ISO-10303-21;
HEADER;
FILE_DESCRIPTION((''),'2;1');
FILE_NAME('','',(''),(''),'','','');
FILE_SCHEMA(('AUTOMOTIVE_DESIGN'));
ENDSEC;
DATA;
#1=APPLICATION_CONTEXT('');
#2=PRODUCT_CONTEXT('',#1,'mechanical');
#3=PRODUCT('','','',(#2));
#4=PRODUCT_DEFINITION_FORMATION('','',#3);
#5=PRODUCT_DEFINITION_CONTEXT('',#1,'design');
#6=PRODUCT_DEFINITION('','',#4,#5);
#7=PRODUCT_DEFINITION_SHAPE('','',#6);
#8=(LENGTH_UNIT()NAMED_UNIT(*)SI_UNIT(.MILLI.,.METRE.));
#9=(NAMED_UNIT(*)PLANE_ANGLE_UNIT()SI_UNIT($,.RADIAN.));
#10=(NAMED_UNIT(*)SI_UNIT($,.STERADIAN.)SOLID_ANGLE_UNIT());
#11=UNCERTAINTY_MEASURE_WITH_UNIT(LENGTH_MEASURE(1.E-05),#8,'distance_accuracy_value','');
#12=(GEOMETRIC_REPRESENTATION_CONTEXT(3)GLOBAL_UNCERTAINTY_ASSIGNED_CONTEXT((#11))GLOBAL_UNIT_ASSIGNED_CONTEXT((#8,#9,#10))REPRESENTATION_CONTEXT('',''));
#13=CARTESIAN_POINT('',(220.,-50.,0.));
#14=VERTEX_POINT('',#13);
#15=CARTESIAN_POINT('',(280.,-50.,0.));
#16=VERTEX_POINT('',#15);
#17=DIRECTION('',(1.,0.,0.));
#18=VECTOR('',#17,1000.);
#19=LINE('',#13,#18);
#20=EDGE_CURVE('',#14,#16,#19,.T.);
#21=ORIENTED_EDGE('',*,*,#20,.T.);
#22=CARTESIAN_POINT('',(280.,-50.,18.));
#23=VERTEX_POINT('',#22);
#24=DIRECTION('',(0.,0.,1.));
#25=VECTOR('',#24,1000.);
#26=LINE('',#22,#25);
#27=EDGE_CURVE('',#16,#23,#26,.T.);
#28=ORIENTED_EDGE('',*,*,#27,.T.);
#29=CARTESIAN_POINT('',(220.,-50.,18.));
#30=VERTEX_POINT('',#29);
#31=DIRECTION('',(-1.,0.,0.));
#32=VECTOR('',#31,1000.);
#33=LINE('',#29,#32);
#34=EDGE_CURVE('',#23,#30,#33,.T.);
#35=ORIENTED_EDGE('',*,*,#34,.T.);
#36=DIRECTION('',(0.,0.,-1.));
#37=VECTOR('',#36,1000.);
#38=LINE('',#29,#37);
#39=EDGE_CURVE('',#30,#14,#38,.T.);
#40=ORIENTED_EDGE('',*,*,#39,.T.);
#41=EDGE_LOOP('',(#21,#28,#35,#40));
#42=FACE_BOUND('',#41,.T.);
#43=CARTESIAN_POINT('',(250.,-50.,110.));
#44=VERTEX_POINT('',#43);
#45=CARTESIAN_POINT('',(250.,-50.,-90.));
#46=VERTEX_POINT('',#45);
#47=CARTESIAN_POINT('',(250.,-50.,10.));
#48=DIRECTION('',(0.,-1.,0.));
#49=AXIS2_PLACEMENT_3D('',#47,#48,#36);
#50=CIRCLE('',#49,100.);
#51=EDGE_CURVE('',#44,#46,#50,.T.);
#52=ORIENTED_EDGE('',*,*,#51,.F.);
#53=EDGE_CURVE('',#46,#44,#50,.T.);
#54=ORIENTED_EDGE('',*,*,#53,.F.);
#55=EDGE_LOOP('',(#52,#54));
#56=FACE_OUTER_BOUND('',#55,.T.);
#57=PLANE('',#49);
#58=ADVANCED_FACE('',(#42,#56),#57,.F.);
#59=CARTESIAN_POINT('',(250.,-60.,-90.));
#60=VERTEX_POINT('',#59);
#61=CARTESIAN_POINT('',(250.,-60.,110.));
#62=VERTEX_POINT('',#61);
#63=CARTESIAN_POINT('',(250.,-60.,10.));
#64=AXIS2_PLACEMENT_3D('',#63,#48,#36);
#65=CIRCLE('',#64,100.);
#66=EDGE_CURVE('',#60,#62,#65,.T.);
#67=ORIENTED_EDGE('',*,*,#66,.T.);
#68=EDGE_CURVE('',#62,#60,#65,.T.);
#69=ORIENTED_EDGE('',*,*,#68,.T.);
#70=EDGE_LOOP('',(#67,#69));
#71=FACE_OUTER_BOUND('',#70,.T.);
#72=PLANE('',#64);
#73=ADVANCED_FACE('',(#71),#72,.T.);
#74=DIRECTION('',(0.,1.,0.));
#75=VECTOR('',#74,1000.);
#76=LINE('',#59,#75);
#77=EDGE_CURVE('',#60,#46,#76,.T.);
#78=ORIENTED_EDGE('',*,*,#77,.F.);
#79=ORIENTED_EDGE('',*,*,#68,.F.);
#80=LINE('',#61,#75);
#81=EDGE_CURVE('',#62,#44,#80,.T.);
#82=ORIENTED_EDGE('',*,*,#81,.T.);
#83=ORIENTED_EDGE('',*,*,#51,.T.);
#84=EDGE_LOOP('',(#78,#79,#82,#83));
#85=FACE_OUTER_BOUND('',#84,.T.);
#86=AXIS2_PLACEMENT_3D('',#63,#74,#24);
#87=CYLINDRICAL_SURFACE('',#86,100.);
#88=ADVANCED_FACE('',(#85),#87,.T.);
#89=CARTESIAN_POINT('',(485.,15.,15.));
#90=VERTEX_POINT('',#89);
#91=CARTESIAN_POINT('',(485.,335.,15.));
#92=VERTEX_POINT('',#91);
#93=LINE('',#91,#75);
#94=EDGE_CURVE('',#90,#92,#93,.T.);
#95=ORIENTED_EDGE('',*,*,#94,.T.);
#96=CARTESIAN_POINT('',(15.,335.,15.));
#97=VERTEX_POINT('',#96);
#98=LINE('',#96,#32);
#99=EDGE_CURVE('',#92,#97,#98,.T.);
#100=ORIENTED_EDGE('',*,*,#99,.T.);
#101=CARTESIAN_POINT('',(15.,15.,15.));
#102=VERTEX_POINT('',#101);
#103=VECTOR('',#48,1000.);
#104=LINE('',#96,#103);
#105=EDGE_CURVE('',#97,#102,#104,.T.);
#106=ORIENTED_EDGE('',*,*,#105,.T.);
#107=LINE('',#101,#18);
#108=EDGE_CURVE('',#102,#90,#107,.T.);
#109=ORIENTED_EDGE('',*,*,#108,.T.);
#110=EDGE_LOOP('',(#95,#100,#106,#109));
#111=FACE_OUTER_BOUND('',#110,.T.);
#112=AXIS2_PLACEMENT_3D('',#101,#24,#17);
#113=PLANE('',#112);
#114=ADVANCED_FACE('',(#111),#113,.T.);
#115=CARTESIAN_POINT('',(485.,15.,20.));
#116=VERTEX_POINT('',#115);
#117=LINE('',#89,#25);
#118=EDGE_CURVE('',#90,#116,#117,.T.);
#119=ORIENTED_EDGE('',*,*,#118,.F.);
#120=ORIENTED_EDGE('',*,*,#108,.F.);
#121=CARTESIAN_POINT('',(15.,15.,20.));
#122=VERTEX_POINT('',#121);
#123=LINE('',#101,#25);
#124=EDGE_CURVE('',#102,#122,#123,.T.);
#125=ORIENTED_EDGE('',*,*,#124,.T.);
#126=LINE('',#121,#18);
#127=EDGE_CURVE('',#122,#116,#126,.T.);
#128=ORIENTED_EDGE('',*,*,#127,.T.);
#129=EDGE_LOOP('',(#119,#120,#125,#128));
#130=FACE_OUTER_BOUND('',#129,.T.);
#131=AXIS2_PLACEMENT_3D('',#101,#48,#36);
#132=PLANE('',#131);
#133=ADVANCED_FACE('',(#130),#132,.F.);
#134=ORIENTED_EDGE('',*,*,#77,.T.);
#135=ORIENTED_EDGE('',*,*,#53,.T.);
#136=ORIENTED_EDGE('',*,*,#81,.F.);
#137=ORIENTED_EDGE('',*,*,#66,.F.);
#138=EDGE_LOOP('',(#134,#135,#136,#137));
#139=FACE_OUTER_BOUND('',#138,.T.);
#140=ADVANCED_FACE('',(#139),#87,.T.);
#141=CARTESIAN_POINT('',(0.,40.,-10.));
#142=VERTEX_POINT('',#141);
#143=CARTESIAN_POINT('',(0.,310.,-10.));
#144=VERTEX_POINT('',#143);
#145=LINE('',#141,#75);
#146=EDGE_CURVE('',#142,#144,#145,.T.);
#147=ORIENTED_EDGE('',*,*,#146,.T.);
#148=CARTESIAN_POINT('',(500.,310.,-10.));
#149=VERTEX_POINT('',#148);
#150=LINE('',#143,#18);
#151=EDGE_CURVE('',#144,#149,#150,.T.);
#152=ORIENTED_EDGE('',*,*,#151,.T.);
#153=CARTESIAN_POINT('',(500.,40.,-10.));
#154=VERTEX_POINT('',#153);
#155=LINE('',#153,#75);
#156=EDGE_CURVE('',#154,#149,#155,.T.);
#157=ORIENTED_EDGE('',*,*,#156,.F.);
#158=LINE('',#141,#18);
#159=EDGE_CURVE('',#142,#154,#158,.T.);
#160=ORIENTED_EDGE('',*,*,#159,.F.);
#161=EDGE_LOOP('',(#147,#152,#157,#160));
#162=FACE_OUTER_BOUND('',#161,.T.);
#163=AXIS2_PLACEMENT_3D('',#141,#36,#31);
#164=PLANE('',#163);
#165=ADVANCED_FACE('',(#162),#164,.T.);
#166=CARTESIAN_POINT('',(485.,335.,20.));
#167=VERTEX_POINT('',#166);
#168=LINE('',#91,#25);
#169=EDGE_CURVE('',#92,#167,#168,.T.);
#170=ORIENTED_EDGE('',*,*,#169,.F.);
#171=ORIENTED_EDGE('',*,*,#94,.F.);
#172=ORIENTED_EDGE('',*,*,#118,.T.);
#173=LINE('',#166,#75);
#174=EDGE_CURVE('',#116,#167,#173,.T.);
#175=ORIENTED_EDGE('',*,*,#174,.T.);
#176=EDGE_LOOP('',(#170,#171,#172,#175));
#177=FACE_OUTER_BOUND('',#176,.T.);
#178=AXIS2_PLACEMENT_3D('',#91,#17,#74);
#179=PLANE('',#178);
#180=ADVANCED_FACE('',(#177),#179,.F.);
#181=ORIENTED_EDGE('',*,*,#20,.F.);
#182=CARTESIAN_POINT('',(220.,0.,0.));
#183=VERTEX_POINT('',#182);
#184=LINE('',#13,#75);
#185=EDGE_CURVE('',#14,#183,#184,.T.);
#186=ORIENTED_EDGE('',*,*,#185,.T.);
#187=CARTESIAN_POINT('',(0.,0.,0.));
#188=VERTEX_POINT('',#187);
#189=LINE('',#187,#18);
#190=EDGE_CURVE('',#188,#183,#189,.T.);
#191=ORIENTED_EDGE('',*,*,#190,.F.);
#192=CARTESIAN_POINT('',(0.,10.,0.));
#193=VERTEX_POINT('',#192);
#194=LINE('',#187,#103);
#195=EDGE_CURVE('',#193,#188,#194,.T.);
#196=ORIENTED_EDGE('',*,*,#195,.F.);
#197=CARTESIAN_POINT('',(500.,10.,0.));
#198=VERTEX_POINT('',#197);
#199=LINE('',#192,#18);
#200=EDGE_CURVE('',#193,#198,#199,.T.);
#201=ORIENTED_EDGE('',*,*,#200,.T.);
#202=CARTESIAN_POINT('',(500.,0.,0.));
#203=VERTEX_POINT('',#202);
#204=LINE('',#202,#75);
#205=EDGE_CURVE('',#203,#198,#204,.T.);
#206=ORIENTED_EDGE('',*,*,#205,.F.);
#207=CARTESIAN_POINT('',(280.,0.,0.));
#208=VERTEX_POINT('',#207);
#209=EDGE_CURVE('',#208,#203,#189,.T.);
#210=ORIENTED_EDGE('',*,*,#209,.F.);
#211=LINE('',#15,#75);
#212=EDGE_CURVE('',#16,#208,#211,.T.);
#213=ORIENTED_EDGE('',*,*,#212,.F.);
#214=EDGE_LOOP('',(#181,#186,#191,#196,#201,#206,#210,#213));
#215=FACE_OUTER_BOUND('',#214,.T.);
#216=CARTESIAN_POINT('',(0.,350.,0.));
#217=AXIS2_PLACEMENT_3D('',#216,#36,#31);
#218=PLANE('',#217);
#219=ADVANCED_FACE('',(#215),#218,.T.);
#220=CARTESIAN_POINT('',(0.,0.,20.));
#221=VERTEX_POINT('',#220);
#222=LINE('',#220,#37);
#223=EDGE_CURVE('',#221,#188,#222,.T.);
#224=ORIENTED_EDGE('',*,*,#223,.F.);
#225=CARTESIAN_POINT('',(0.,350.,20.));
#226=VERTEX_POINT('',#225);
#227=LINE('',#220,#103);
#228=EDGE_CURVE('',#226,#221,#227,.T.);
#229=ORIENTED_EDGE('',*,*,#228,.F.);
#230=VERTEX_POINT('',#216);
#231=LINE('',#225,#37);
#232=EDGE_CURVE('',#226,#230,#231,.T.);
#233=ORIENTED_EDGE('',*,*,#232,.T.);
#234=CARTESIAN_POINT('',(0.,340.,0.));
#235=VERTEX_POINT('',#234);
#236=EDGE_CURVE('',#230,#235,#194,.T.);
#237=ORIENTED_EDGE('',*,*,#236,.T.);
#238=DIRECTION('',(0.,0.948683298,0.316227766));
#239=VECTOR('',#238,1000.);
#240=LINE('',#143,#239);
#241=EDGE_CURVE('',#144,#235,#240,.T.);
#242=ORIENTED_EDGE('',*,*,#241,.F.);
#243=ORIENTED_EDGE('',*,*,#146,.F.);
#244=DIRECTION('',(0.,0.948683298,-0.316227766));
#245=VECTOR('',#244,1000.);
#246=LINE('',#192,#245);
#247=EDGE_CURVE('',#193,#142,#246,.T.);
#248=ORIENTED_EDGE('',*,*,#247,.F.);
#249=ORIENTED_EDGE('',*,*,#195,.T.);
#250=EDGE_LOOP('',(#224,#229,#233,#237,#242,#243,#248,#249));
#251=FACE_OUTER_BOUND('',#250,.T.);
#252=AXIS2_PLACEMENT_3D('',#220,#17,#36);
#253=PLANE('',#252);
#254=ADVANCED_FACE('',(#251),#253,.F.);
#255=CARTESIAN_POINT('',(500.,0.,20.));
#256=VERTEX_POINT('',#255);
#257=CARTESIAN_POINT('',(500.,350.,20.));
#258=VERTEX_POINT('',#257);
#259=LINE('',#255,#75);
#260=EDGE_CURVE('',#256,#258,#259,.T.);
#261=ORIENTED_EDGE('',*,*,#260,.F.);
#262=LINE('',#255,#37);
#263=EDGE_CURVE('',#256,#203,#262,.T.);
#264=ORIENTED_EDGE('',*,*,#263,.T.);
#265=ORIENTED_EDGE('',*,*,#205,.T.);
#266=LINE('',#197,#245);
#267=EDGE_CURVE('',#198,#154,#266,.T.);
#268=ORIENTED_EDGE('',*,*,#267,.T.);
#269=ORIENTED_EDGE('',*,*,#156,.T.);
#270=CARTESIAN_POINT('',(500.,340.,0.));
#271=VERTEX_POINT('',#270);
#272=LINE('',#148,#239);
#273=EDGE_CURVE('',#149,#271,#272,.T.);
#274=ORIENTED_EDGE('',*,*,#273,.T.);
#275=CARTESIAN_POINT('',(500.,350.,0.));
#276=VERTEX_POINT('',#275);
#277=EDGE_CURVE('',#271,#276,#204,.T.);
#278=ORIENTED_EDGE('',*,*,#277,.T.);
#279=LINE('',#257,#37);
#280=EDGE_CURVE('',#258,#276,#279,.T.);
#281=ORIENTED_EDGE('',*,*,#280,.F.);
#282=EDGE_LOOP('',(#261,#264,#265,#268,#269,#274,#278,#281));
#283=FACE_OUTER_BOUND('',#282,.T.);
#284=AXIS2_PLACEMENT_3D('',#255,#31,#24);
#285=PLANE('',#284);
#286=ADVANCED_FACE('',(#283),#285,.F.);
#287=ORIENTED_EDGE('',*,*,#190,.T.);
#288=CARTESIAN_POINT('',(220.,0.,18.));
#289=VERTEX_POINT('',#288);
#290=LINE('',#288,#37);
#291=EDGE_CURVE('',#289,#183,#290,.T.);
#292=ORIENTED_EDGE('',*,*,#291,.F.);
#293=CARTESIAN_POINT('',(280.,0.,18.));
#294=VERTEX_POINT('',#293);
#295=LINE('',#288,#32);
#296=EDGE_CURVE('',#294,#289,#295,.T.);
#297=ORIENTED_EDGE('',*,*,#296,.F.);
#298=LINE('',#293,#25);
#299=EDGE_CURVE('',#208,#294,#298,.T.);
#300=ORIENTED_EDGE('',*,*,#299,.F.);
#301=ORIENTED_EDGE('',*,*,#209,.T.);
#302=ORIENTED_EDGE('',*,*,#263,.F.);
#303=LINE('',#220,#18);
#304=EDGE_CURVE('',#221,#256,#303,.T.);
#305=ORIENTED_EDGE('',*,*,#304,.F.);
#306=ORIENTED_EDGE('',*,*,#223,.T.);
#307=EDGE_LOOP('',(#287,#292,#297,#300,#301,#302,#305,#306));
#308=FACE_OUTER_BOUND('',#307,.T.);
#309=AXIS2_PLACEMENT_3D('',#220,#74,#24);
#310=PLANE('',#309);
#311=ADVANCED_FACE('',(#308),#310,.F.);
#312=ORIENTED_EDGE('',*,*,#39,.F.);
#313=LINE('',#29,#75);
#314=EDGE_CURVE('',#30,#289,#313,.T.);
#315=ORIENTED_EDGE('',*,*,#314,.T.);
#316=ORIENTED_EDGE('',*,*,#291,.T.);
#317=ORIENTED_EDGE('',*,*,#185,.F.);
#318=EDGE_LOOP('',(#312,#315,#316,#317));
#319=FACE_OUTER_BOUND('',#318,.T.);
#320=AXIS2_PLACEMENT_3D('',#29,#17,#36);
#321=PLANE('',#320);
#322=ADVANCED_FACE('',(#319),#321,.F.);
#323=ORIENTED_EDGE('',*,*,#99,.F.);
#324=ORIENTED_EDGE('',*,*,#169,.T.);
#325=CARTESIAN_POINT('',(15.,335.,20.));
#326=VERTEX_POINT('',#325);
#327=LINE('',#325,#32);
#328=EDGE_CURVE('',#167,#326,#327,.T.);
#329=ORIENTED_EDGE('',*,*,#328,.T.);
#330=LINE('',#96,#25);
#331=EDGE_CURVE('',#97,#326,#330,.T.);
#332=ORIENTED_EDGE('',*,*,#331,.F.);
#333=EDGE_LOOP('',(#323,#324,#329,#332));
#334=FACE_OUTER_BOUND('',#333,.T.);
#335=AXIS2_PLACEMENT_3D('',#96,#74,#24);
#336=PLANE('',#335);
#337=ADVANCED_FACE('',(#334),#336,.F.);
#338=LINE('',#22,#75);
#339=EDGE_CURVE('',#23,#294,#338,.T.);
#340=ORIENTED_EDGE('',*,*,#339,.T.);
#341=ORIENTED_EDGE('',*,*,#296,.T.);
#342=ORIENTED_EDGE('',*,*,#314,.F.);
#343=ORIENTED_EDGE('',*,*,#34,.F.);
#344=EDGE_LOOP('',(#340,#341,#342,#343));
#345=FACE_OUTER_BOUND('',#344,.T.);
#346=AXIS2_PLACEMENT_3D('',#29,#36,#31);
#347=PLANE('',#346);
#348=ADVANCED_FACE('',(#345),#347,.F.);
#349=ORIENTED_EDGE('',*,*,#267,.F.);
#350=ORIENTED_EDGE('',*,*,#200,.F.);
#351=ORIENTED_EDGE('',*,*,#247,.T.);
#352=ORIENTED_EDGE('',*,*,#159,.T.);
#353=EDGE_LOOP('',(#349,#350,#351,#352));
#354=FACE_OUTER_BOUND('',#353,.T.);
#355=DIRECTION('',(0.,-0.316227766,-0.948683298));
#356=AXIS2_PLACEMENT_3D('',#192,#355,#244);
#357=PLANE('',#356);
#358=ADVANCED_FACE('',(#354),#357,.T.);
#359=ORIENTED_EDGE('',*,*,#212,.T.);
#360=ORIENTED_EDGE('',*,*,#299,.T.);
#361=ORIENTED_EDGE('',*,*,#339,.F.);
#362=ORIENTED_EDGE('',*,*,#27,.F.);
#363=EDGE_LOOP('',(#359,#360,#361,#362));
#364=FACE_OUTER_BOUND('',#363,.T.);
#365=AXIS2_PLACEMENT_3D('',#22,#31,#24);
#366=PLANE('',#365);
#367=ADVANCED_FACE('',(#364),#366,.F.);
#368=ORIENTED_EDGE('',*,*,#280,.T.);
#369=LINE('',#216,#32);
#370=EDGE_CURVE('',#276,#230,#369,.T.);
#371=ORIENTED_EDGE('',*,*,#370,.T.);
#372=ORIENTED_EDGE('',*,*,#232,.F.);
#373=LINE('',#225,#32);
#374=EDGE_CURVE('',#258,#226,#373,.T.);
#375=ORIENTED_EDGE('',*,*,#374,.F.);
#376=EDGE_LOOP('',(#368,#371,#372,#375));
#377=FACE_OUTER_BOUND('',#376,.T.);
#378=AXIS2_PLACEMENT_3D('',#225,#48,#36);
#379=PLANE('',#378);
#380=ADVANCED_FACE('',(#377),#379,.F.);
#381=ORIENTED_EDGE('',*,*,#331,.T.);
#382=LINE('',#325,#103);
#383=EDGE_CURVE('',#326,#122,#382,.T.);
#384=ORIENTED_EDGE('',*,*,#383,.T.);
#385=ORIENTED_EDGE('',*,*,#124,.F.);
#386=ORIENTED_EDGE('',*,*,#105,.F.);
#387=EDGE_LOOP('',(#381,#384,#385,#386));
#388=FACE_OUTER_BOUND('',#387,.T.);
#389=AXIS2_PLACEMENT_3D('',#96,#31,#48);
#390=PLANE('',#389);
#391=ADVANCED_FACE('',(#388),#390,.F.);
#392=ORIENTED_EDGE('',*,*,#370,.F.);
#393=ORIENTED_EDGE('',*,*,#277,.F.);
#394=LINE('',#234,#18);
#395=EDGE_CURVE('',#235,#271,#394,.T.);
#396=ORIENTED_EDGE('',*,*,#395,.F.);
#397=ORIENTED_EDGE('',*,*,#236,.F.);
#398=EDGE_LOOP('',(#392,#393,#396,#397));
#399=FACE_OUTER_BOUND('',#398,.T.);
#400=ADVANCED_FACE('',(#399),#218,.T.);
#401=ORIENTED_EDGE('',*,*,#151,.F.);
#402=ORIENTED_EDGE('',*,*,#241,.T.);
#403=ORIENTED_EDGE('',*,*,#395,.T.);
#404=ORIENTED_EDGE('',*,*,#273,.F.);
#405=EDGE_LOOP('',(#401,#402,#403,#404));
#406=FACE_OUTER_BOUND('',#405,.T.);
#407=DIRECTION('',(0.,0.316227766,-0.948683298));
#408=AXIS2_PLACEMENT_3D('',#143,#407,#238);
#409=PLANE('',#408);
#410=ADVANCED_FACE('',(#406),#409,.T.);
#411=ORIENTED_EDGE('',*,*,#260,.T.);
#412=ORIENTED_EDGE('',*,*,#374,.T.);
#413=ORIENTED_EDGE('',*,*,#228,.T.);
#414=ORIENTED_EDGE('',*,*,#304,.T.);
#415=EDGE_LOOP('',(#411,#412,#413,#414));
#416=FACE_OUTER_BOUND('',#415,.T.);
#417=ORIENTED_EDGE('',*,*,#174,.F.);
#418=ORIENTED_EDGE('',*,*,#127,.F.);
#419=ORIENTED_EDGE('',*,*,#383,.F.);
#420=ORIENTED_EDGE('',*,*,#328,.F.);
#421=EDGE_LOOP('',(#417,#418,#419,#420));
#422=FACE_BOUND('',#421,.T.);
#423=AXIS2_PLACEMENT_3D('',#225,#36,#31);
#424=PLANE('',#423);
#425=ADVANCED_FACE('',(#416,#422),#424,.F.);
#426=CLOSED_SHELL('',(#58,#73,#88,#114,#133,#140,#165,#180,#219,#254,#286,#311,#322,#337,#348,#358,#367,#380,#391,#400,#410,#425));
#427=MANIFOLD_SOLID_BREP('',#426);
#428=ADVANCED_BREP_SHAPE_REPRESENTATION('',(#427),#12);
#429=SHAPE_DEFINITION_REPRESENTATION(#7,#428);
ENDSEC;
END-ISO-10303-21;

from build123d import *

# Parameters (mm, degrees)
SKETCH1_W           = 500
SKETCH1_H           = 350
BOSS_EXTRUDE1_DEPTH = 20
BOSS_EXTRUDE2_DEPTH = 500
SKETCH3_W           = 470
SKETCH3_H           = 320
CUT_EXTRUDE1_DEPTH  = 5
SKETCH4_W           = 60
SKETCH4_H           = 18
BOSS_EXTRUDE3_DEPTH = 50
SKETCH5_R           = 100
BOSS_EXTRUDE4_DEPTH = 10


with BuildPart() as part:
    # Sketch1 → Boss-Extrude1 (new body)
    with BuildSketch(Plane.XY):
        with Locations((250, 175)):
            Rectangle(SKETCH1_W, SKETCH1_H)
    extrude(amount=BOSS_EXTRUDE1_DEPTH)

    # Sketch2 → Boss-Extrude2 (add)
    with BuildSketch(Plane(origin=(500, 0, 0), x_dir=(0, 0, -1), z_dir=(1, 0, 0))):
        Polygon((0, 340), (0, 10), (10, 40), (10, 310), align=None)
    extrude(amount=-BOSS_EXTRUDE2_DEPTH)

    # Sketch3 → Cut-Extrude1 (cut)
    with BuildSketch(Plane.XY.offset(20)):
        with Locations((250, 175)):
            Rectangle(SKETCH3_W, SKETCH3_H)
    extrude(amount=-CUT_EXTRUDE1_DEPTH, mode=Mode.SUBTRACT)

    # Sketch4 → Boss-Extrude3 (add)
    with BuildSketch(Plane.XZ):
        with Locations((250, 9)):
            Rectangle(SKETCH4_W, SKETCH4_H)
    extrude(amount=BOSS_EXTRUDE3_DEPTH)

    # Sketch5 → Boss-Extrude4 (add)
    with BuildSketch(Plane.XZ.offset(50)):
        with Locations(Location((250, 10, 0), (0, 0, 270))):
            Circle(SKETCH5_R)
    extrude(amount=BOSS_EXTRUDE4_DEPTH)


solid = part.part
